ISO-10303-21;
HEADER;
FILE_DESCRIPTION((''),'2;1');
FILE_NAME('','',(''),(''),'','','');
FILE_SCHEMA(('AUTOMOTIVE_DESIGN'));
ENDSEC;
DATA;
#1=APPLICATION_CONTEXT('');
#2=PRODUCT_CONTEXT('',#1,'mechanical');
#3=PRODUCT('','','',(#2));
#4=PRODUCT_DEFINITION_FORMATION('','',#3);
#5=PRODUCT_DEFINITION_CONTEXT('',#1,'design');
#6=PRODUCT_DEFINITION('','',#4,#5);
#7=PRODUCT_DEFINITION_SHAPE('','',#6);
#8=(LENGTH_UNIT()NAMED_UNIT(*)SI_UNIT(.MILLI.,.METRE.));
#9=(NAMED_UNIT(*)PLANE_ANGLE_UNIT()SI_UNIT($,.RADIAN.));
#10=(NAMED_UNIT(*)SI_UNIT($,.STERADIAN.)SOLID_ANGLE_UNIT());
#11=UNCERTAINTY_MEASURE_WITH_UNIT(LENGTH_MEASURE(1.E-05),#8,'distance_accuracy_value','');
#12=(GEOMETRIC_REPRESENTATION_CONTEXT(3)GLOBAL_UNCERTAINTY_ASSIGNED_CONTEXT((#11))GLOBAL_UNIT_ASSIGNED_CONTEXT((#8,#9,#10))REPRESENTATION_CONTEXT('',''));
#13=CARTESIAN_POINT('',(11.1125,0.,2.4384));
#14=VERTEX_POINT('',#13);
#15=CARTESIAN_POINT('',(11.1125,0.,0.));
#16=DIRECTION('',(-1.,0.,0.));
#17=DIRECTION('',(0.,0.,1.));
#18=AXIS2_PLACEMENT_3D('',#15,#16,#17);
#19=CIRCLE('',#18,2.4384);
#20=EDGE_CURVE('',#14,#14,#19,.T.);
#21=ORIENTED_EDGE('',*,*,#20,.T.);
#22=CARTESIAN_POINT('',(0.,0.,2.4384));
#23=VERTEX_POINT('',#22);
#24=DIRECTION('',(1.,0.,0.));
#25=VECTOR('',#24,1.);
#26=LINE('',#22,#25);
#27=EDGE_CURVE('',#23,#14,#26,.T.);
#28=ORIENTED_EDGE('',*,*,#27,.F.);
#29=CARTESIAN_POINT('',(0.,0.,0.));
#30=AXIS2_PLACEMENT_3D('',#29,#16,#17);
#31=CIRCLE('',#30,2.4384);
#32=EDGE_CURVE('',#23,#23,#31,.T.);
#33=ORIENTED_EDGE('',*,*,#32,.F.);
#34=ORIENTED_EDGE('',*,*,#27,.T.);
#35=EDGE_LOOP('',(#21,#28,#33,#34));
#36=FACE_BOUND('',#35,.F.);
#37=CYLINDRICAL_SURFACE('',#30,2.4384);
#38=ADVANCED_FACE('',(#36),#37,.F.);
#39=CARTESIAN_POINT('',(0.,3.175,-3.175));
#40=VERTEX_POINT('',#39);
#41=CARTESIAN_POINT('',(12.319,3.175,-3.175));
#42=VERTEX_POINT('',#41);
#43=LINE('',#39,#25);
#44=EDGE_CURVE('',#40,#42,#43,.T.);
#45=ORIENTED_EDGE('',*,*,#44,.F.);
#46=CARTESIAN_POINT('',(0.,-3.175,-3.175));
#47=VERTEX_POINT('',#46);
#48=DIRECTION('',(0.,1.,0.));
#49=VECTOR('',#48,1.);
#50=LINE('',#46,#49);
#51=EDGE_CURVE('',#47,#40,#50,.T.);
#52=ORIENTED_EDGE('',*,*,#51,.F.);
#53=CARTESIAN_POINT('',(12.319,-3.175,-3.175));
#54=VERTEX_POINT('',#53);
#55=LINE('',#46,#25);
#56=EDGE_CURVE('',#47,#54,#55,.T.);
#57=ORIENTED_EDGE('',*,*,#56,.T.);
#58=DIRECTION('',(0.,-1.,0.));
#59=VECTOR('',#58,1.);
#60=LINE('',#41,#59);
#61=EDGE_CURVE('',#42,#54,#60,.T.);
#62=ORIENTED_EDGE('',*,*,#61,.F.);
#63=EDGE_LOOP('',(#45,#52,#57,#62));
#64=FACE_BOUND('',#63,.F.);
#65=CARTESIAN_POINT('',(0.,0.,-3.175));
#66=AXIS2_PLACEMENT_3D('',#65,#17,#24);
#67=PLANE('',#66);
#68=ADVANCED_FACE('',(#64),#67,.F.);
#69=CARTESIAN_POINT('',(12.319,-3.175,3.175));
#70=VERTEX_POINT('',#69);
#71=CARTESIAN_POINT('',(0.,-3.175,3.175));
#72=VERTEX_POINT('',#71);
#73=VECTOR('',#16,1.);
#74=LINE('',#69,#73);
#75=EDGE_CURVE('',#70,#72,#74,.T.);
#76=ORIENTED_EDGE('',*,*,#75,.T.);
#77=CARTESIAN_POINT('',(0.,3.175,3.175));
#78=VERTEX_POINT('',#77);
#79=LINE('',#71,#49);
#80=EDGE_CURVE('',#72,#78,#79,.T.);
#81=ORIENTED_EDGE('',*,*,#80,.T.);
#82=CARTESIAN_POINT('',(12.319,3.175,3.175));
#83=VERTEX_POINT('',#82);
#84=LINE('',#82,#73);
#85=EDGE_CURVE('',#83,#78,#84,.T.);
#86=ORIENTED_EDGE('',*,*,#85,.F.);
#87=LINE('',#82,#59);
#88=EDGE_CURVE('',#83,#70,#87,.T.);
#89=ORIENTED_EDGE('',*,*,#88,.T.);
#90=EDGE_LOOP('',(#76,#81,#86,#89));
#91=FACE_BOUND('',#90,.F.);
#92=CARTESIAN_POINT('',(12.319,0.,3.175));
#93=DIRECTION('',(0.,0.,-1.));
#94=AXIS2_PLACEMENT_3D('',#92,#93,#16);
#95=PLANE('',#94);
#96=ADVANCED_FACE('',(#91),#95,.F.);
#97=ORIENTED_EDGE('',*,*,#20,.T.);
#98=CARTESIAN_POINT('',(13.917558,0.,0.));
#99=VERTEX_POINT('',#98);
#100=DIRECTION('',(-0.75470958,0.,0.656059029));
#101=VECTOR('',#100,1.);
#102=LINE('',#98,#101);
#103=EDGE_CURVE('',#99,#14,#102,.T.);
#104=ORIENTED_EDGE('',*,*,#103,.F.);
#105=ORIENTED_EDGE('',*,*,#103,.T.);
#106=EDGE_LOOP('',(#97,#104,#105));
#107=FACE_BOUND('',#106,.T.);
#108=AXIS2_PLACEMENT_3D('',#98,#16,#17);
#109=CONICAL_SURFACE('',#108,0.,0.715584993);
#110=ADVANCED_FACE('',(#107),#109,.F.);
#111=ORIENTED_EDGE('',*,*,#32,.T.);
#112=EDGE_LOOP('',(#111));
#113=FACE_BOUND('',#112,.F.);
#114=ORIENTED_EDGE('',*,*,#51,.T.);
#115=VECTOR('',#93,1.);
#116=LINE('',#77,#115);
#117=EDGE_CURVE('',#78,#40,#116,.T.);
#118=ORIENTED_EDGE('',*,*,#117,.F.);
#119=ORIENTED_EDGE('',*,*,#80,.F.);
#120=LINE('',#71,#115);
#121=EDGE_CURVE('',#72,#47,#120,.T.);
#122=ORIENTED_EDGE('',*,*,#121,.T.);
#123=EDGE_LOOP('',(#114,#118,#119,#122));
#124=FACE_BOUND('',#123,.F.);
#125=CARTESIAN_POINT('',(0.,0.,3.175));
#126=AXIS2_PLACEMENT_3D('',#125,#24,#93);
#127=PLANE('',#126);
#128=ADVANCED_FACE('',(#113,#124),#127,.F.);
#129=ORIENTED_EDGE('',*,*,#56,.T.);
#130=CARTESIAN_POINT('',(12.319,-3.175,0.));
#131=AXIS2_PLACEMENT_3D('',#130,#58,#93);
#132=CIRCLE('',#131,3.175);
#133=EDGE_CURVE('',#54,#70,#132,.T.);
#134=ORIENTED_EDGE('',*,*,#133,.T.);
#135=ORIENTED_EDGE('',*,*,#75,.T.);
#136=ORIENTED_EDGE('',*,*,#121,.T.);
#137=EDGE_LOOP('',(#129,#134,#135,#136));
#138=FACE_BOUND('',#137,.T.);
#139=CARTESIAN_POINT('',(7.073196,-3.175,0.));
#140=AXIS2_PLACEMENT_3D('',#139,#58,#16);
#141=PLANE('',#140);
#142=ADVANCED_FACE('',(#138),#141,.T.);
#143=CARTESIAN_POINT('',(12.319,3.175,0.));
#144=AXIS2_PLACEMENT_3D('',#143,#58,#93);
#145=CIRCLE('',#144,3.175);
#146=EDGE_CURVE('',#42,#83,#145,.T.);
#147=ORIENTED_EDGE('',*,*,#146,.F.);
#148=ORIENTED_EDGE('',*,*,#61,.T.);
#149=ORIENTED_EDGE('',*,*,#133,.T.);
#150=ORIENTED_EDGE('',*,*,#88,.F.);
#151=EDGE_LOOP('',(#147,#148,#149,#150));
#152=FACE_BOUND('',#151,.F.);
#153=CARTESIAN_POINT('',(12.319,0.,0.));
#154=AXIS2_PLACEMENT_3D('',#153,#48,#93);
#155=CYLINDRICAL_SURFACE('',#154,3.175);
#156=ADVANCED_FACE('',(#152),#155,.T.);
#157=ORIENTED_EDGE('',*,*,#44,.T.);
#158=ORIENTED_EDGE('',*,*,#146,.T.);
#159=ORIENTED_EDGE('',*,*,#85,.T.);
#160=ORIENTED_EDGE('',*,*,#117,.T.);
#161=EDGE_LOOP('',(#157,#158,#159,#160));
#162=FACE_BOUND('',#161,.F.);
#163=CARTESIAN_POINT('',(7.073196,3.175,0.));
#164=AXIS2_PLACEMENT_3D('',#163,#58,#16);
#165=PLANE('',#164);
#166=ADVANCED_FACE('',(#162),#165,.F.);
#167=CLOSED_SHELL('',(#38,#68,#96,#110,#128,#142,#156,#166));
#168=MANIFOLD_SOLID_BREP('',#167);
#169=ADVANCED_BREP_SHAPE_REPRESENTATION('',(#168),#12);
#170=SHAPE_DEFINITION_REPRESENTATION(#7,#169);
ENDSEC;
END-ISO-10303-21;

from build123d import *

# Parameters (mm, degrees)
BOSS_EXTRUDE1_DEPTH = 3.175
SKETCH2_R           = 2.4384
CUT_EXTRUDE1_DEPTH  = 11.1125


with BuildPart() as part:
    # Sketch1 → Boss-Extrude1 (new, symmetric)
    with BuildSketch(Plane(origin=(0, 0, 0), x_dir=(1, 0, 0), z_dir=(0, 1, 0))):
        with BuildLine():
            Line((0, 3.175), (12.319, 3.175))
            ThreePointArc((12.319, 3.175), (15.494, 0), (12.319, -3.175))
            Line((12.319, -3.175), (0, -3.175))
            Line((0, -3.175), (0, 3.175))
        make_face()
    extrude(amount=BOSS_EXTRUDE1_DEPTH, both=True)

    # Sketch2 → Cut-Extrude1 (cut)
    with BuildSketch(Plane.ZY):
        Circle(SKETCH2_R)
    extrude(amount=-CUT_EXTRUDE1_DEPTH, mode=Mode.SUBTRACT)

    # Sketch3 → Cut-Revolve1 (revolve, cut)
    with BuildSketch(Plane(origin=(0, 0, 0), x_dir=(1, 0, 0), z_dir=(0, 1, 0))):
        Polygon((13.917558324, 0), (11.1125, -2.4384), (0, -2.4384), (0, 0), align=None)
    revolve(axis=Axis((0, 0, 0), (1, 0, 0)), mode=Mode.SUBTRACT)


solid = part.part
